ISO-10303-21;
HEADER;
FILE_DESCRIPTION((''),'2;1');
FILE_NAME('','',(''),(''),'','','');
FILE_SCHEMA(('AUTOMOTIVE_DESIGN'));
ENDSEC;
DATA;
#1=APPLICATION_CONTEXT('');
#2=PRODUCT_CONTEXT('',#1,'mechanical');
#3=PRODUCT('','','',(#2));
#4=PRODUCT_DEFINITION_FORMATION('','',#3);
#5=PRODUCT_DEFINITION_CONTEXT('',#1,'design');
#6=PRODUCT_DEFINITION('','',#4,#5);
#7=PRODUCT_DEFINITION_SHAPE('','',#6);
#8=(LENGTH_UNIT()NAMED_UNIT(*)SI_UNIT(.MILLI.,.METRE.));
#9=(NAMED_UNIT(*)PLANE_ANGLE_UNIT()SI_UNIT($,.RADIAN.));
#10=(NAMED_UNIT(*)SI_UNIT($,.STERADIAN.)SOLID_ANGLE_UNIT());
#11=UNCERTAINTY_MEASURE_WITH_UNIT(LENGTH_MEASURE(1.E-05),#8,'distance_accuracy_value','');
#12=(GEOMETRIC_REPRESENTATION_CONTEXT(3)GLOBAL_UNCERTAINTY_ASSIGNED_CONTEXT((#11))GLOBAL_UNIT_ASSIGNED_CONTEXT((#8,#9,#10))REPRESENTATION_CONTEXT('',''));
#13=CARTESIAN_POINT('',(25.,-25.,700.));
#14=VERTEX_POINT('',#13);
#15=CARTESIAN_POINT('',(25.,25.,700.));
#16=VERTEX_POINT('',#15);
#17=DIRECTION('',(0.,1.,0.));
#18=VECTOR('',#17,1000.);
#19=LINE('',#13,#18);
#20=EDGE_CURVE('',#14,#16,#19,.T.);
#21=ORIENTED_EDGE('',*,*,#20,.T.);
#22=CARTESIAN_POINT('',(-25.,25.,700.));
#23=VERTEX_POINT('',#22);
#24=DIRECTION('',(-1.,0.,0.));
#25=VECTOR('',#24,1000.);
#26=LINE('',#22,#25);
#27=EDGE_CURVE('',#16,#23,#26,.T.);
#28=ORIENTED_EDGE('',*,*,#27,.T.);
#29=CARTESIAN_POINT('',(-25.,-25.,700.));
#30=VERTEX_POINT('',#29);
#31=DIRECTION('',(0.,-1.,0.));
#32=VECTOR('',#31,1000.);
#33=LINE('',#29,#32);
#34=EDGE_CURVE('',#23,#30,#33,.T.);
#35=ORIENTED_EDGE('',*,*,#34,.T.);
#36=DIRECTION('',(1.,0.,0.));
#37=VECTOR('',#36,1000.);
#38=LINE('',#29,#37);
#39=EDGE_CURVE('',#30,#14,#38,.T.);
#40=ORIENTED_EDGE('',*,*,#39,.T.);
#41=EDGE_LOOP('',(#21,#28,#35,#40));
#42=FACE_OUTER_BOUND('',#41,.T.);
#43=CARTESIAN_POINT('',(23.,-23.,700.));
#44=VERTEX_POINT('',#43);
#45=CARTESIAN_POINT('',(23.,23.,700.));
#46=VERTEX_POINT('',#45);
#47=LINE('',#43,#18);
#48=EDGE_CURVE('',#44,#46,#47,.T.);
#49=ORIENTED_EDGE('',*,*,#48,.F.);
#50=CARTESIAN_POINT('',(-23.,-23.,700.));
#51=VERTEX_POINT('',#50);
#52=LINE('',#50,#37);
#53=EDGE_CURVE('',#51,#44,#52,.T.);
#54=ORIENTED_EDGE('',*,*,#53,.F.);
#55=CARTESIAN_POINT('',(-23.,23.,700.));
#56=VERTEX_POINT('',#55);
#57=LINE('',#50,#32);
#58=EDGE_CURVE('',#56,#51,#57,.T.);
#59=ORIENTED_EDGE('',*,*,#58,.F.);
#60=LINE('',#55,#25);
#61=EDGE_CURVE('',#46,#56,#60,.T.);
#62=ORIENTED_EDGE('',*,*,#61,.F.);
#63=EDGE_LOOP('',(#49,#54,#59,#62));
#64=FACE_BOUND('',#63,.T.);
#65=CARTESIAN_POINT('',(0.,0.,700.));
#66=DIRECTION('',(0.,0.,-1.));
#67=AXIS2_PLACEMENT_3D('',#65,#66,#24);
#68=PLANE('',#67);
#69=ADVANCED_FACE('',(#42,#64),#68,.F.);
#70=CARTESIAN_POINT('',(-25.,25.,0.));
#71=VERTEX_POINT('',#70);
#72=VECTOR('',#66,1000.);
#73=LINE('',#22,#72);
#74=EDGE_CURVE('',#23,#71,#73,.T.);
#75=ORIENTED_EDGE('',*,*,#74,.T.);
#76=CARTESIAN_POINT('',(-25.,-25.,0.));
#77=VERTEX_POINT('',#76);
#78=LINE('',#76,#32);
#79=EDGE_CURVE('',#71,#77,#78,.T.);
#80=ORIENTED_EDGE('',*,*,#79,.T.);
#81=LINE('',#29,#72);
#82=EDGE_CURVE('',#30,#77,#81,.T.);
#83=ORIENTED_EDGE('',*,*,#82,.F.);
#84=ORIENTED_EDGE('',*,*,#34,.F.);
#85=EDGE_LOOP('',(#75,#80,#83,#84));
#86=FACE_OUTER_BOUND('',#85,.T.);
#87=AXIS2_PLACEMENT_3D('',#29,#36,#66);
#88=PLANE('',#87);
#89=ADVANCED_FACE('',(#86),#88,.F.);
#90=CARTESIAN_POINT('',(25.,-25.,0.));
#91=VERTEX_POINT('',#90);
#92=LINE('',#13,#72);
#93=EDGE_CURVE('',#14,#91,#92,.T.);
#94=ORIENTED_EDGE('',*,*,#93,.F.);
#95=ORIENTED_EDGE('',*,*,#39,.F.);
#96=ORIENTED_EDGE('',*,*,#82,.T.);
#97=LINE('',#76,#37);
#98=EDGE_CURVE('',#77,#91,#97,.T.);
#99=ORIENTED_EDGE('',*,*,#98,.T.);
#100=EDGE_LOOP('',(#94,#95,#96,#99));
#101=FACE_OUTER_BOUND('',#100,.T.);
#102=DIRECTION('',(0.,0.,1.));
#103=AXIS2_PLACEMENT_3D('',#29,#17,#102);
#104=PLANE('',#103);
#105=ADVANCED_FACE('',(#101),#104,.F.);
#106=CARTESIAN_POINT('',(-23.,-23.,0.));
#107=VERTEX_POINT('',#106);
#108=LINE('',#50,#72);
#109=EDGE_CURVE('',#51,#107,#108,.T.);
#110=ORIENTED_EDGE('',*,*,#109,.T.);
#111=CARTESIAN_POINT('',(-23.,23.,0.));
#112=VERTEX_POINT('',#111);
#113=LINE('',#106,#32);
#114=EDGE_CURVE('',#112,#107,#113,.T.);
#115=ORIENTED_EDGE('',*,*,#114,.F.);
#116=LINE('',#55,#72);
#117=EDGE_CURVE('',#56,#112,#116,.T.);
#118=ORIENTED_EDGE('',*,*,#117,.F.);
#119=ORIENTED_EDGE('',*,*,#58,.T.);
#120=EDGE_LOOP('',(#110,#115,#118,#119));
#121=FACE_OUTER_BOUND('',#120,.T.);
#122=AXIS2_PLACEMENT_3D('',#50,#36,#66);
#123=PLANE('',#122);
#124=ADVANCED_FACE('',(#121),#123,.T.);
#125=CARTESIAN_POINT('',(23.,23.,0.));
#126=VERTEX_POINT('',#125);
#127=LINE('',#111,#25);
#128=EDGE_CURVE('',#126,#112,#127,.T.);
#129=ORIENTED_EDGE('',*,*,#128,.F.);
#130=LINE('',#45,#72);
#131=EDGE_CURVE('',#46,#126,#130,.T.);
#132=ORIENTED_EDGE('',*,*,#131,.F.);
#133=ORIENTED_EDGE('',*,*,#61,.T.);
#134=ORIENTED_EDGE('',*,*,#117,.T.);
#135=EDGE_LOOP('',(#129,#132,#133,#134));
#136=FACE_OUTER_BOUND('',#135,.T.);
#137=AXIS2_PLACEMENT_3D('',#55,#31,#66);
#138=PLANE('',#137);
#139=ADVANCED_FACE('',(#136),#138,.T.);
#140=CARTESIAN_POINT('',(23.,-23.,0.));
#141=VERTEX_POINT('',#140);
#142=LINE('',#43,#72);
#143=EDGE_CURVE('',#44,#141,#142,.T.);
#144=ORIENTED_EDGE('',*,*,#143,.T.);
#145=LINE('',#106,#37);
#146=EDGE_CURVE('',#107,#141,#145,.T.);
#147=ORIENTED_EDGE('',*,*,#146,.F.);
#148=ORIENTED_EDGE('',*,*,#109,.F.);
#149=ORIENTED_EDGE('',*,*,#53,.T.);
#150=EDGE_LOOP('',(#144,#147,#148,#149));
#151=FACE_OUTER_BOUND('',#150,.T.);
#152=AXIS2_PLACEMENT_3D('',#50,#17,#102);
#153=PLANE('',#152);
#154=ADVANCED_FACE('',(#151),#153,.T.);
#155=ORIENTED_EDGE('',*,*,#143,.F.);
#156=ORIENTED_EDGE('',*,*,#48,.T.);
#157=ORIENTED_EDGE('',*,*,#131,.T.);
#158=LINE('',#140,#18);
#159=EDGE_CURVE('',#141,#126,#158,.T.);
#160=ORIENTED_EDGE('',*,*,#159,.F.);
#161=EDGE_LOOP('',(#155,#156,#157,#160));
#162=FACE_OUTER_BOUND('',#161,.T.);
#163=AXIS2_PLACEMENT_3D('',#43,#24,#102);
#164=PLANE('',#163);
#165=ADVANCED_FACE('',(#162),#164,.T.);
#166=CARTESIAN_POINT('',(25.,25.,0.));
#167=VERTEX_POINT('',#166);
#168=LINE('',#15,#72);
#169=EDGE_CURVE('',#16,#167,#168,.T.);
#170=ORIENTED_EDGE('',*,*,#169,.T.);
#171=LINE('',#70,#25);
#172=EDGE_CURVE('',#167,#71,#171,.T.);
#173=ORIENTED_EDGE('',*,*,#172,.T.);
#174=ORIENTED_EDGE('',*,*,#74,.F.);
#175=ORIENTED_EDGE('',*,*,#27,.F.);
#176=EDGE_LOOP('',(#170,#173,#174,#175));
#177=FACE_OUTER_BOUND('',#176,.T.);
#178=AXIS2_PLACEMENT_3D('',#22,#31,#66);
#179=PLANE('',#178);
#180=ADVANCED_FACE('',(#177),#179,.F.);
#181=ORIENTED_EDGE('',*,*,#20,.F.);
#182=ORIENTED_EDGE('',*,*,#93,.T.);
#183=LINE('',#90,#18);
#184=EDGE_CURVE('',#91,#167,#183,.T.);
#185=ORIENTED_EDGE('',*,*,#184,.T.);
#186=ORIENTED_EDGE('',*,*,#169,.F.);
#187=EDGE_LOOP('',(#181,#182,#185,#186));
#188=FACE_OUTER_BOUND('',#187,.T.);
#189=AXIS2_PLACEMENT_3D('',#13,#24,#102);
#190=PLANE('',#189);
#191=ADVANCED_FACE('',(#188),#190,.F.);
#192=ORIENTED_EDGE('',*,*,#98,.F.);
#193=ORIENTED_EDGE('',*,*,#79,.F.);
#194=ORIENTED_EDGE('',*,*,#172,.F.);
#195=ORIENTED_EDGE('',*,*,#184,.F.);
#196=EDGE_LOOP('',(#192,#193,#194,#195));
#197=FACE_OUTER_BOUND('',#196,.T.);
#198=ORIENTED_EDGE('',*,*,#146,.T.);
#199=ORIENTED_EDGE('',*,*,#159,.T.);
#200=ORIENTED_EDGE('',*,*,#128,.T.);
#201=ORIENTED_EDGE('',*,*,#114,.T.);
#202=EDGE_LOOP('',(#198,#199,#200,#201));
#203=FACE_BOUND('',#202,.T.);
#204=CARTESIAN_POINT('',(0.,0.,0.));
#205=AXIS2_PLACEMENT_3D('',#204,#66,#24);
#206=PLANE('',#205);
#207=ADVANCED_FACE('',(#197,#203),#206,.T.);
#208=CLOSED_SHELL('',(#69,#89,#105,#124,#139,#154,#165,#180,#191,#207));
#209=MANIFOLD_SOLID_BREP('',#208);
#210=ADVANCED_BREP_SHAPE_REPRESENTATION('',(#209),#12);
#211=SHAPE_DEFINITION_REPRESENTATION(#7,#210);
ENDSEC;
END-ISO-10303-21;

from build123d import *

# Parameters (mm, degrees)
SKETCH1_W           = 50
SKETCH1_H           = 50
SKETCH1_W_2         = 46
SKETCH1_H_2         = 46
BOSS_EXTRUDE1_DEPTH = 700


with BuildPart() as part:
    # Sketch1 → Boss-Extrude1 (new body)
    with BuildSketch(Plane.XY):
        Rectangle(SKETCH1_W, SKETCH1_H)
        Rectangle(SKETCH1_W_2, SKETCH1_H_2, mode=Mode.SUBTRACT)
    extrude(amount=BOSS_EXTRUDE1_DEPTH)


solid = part.part
